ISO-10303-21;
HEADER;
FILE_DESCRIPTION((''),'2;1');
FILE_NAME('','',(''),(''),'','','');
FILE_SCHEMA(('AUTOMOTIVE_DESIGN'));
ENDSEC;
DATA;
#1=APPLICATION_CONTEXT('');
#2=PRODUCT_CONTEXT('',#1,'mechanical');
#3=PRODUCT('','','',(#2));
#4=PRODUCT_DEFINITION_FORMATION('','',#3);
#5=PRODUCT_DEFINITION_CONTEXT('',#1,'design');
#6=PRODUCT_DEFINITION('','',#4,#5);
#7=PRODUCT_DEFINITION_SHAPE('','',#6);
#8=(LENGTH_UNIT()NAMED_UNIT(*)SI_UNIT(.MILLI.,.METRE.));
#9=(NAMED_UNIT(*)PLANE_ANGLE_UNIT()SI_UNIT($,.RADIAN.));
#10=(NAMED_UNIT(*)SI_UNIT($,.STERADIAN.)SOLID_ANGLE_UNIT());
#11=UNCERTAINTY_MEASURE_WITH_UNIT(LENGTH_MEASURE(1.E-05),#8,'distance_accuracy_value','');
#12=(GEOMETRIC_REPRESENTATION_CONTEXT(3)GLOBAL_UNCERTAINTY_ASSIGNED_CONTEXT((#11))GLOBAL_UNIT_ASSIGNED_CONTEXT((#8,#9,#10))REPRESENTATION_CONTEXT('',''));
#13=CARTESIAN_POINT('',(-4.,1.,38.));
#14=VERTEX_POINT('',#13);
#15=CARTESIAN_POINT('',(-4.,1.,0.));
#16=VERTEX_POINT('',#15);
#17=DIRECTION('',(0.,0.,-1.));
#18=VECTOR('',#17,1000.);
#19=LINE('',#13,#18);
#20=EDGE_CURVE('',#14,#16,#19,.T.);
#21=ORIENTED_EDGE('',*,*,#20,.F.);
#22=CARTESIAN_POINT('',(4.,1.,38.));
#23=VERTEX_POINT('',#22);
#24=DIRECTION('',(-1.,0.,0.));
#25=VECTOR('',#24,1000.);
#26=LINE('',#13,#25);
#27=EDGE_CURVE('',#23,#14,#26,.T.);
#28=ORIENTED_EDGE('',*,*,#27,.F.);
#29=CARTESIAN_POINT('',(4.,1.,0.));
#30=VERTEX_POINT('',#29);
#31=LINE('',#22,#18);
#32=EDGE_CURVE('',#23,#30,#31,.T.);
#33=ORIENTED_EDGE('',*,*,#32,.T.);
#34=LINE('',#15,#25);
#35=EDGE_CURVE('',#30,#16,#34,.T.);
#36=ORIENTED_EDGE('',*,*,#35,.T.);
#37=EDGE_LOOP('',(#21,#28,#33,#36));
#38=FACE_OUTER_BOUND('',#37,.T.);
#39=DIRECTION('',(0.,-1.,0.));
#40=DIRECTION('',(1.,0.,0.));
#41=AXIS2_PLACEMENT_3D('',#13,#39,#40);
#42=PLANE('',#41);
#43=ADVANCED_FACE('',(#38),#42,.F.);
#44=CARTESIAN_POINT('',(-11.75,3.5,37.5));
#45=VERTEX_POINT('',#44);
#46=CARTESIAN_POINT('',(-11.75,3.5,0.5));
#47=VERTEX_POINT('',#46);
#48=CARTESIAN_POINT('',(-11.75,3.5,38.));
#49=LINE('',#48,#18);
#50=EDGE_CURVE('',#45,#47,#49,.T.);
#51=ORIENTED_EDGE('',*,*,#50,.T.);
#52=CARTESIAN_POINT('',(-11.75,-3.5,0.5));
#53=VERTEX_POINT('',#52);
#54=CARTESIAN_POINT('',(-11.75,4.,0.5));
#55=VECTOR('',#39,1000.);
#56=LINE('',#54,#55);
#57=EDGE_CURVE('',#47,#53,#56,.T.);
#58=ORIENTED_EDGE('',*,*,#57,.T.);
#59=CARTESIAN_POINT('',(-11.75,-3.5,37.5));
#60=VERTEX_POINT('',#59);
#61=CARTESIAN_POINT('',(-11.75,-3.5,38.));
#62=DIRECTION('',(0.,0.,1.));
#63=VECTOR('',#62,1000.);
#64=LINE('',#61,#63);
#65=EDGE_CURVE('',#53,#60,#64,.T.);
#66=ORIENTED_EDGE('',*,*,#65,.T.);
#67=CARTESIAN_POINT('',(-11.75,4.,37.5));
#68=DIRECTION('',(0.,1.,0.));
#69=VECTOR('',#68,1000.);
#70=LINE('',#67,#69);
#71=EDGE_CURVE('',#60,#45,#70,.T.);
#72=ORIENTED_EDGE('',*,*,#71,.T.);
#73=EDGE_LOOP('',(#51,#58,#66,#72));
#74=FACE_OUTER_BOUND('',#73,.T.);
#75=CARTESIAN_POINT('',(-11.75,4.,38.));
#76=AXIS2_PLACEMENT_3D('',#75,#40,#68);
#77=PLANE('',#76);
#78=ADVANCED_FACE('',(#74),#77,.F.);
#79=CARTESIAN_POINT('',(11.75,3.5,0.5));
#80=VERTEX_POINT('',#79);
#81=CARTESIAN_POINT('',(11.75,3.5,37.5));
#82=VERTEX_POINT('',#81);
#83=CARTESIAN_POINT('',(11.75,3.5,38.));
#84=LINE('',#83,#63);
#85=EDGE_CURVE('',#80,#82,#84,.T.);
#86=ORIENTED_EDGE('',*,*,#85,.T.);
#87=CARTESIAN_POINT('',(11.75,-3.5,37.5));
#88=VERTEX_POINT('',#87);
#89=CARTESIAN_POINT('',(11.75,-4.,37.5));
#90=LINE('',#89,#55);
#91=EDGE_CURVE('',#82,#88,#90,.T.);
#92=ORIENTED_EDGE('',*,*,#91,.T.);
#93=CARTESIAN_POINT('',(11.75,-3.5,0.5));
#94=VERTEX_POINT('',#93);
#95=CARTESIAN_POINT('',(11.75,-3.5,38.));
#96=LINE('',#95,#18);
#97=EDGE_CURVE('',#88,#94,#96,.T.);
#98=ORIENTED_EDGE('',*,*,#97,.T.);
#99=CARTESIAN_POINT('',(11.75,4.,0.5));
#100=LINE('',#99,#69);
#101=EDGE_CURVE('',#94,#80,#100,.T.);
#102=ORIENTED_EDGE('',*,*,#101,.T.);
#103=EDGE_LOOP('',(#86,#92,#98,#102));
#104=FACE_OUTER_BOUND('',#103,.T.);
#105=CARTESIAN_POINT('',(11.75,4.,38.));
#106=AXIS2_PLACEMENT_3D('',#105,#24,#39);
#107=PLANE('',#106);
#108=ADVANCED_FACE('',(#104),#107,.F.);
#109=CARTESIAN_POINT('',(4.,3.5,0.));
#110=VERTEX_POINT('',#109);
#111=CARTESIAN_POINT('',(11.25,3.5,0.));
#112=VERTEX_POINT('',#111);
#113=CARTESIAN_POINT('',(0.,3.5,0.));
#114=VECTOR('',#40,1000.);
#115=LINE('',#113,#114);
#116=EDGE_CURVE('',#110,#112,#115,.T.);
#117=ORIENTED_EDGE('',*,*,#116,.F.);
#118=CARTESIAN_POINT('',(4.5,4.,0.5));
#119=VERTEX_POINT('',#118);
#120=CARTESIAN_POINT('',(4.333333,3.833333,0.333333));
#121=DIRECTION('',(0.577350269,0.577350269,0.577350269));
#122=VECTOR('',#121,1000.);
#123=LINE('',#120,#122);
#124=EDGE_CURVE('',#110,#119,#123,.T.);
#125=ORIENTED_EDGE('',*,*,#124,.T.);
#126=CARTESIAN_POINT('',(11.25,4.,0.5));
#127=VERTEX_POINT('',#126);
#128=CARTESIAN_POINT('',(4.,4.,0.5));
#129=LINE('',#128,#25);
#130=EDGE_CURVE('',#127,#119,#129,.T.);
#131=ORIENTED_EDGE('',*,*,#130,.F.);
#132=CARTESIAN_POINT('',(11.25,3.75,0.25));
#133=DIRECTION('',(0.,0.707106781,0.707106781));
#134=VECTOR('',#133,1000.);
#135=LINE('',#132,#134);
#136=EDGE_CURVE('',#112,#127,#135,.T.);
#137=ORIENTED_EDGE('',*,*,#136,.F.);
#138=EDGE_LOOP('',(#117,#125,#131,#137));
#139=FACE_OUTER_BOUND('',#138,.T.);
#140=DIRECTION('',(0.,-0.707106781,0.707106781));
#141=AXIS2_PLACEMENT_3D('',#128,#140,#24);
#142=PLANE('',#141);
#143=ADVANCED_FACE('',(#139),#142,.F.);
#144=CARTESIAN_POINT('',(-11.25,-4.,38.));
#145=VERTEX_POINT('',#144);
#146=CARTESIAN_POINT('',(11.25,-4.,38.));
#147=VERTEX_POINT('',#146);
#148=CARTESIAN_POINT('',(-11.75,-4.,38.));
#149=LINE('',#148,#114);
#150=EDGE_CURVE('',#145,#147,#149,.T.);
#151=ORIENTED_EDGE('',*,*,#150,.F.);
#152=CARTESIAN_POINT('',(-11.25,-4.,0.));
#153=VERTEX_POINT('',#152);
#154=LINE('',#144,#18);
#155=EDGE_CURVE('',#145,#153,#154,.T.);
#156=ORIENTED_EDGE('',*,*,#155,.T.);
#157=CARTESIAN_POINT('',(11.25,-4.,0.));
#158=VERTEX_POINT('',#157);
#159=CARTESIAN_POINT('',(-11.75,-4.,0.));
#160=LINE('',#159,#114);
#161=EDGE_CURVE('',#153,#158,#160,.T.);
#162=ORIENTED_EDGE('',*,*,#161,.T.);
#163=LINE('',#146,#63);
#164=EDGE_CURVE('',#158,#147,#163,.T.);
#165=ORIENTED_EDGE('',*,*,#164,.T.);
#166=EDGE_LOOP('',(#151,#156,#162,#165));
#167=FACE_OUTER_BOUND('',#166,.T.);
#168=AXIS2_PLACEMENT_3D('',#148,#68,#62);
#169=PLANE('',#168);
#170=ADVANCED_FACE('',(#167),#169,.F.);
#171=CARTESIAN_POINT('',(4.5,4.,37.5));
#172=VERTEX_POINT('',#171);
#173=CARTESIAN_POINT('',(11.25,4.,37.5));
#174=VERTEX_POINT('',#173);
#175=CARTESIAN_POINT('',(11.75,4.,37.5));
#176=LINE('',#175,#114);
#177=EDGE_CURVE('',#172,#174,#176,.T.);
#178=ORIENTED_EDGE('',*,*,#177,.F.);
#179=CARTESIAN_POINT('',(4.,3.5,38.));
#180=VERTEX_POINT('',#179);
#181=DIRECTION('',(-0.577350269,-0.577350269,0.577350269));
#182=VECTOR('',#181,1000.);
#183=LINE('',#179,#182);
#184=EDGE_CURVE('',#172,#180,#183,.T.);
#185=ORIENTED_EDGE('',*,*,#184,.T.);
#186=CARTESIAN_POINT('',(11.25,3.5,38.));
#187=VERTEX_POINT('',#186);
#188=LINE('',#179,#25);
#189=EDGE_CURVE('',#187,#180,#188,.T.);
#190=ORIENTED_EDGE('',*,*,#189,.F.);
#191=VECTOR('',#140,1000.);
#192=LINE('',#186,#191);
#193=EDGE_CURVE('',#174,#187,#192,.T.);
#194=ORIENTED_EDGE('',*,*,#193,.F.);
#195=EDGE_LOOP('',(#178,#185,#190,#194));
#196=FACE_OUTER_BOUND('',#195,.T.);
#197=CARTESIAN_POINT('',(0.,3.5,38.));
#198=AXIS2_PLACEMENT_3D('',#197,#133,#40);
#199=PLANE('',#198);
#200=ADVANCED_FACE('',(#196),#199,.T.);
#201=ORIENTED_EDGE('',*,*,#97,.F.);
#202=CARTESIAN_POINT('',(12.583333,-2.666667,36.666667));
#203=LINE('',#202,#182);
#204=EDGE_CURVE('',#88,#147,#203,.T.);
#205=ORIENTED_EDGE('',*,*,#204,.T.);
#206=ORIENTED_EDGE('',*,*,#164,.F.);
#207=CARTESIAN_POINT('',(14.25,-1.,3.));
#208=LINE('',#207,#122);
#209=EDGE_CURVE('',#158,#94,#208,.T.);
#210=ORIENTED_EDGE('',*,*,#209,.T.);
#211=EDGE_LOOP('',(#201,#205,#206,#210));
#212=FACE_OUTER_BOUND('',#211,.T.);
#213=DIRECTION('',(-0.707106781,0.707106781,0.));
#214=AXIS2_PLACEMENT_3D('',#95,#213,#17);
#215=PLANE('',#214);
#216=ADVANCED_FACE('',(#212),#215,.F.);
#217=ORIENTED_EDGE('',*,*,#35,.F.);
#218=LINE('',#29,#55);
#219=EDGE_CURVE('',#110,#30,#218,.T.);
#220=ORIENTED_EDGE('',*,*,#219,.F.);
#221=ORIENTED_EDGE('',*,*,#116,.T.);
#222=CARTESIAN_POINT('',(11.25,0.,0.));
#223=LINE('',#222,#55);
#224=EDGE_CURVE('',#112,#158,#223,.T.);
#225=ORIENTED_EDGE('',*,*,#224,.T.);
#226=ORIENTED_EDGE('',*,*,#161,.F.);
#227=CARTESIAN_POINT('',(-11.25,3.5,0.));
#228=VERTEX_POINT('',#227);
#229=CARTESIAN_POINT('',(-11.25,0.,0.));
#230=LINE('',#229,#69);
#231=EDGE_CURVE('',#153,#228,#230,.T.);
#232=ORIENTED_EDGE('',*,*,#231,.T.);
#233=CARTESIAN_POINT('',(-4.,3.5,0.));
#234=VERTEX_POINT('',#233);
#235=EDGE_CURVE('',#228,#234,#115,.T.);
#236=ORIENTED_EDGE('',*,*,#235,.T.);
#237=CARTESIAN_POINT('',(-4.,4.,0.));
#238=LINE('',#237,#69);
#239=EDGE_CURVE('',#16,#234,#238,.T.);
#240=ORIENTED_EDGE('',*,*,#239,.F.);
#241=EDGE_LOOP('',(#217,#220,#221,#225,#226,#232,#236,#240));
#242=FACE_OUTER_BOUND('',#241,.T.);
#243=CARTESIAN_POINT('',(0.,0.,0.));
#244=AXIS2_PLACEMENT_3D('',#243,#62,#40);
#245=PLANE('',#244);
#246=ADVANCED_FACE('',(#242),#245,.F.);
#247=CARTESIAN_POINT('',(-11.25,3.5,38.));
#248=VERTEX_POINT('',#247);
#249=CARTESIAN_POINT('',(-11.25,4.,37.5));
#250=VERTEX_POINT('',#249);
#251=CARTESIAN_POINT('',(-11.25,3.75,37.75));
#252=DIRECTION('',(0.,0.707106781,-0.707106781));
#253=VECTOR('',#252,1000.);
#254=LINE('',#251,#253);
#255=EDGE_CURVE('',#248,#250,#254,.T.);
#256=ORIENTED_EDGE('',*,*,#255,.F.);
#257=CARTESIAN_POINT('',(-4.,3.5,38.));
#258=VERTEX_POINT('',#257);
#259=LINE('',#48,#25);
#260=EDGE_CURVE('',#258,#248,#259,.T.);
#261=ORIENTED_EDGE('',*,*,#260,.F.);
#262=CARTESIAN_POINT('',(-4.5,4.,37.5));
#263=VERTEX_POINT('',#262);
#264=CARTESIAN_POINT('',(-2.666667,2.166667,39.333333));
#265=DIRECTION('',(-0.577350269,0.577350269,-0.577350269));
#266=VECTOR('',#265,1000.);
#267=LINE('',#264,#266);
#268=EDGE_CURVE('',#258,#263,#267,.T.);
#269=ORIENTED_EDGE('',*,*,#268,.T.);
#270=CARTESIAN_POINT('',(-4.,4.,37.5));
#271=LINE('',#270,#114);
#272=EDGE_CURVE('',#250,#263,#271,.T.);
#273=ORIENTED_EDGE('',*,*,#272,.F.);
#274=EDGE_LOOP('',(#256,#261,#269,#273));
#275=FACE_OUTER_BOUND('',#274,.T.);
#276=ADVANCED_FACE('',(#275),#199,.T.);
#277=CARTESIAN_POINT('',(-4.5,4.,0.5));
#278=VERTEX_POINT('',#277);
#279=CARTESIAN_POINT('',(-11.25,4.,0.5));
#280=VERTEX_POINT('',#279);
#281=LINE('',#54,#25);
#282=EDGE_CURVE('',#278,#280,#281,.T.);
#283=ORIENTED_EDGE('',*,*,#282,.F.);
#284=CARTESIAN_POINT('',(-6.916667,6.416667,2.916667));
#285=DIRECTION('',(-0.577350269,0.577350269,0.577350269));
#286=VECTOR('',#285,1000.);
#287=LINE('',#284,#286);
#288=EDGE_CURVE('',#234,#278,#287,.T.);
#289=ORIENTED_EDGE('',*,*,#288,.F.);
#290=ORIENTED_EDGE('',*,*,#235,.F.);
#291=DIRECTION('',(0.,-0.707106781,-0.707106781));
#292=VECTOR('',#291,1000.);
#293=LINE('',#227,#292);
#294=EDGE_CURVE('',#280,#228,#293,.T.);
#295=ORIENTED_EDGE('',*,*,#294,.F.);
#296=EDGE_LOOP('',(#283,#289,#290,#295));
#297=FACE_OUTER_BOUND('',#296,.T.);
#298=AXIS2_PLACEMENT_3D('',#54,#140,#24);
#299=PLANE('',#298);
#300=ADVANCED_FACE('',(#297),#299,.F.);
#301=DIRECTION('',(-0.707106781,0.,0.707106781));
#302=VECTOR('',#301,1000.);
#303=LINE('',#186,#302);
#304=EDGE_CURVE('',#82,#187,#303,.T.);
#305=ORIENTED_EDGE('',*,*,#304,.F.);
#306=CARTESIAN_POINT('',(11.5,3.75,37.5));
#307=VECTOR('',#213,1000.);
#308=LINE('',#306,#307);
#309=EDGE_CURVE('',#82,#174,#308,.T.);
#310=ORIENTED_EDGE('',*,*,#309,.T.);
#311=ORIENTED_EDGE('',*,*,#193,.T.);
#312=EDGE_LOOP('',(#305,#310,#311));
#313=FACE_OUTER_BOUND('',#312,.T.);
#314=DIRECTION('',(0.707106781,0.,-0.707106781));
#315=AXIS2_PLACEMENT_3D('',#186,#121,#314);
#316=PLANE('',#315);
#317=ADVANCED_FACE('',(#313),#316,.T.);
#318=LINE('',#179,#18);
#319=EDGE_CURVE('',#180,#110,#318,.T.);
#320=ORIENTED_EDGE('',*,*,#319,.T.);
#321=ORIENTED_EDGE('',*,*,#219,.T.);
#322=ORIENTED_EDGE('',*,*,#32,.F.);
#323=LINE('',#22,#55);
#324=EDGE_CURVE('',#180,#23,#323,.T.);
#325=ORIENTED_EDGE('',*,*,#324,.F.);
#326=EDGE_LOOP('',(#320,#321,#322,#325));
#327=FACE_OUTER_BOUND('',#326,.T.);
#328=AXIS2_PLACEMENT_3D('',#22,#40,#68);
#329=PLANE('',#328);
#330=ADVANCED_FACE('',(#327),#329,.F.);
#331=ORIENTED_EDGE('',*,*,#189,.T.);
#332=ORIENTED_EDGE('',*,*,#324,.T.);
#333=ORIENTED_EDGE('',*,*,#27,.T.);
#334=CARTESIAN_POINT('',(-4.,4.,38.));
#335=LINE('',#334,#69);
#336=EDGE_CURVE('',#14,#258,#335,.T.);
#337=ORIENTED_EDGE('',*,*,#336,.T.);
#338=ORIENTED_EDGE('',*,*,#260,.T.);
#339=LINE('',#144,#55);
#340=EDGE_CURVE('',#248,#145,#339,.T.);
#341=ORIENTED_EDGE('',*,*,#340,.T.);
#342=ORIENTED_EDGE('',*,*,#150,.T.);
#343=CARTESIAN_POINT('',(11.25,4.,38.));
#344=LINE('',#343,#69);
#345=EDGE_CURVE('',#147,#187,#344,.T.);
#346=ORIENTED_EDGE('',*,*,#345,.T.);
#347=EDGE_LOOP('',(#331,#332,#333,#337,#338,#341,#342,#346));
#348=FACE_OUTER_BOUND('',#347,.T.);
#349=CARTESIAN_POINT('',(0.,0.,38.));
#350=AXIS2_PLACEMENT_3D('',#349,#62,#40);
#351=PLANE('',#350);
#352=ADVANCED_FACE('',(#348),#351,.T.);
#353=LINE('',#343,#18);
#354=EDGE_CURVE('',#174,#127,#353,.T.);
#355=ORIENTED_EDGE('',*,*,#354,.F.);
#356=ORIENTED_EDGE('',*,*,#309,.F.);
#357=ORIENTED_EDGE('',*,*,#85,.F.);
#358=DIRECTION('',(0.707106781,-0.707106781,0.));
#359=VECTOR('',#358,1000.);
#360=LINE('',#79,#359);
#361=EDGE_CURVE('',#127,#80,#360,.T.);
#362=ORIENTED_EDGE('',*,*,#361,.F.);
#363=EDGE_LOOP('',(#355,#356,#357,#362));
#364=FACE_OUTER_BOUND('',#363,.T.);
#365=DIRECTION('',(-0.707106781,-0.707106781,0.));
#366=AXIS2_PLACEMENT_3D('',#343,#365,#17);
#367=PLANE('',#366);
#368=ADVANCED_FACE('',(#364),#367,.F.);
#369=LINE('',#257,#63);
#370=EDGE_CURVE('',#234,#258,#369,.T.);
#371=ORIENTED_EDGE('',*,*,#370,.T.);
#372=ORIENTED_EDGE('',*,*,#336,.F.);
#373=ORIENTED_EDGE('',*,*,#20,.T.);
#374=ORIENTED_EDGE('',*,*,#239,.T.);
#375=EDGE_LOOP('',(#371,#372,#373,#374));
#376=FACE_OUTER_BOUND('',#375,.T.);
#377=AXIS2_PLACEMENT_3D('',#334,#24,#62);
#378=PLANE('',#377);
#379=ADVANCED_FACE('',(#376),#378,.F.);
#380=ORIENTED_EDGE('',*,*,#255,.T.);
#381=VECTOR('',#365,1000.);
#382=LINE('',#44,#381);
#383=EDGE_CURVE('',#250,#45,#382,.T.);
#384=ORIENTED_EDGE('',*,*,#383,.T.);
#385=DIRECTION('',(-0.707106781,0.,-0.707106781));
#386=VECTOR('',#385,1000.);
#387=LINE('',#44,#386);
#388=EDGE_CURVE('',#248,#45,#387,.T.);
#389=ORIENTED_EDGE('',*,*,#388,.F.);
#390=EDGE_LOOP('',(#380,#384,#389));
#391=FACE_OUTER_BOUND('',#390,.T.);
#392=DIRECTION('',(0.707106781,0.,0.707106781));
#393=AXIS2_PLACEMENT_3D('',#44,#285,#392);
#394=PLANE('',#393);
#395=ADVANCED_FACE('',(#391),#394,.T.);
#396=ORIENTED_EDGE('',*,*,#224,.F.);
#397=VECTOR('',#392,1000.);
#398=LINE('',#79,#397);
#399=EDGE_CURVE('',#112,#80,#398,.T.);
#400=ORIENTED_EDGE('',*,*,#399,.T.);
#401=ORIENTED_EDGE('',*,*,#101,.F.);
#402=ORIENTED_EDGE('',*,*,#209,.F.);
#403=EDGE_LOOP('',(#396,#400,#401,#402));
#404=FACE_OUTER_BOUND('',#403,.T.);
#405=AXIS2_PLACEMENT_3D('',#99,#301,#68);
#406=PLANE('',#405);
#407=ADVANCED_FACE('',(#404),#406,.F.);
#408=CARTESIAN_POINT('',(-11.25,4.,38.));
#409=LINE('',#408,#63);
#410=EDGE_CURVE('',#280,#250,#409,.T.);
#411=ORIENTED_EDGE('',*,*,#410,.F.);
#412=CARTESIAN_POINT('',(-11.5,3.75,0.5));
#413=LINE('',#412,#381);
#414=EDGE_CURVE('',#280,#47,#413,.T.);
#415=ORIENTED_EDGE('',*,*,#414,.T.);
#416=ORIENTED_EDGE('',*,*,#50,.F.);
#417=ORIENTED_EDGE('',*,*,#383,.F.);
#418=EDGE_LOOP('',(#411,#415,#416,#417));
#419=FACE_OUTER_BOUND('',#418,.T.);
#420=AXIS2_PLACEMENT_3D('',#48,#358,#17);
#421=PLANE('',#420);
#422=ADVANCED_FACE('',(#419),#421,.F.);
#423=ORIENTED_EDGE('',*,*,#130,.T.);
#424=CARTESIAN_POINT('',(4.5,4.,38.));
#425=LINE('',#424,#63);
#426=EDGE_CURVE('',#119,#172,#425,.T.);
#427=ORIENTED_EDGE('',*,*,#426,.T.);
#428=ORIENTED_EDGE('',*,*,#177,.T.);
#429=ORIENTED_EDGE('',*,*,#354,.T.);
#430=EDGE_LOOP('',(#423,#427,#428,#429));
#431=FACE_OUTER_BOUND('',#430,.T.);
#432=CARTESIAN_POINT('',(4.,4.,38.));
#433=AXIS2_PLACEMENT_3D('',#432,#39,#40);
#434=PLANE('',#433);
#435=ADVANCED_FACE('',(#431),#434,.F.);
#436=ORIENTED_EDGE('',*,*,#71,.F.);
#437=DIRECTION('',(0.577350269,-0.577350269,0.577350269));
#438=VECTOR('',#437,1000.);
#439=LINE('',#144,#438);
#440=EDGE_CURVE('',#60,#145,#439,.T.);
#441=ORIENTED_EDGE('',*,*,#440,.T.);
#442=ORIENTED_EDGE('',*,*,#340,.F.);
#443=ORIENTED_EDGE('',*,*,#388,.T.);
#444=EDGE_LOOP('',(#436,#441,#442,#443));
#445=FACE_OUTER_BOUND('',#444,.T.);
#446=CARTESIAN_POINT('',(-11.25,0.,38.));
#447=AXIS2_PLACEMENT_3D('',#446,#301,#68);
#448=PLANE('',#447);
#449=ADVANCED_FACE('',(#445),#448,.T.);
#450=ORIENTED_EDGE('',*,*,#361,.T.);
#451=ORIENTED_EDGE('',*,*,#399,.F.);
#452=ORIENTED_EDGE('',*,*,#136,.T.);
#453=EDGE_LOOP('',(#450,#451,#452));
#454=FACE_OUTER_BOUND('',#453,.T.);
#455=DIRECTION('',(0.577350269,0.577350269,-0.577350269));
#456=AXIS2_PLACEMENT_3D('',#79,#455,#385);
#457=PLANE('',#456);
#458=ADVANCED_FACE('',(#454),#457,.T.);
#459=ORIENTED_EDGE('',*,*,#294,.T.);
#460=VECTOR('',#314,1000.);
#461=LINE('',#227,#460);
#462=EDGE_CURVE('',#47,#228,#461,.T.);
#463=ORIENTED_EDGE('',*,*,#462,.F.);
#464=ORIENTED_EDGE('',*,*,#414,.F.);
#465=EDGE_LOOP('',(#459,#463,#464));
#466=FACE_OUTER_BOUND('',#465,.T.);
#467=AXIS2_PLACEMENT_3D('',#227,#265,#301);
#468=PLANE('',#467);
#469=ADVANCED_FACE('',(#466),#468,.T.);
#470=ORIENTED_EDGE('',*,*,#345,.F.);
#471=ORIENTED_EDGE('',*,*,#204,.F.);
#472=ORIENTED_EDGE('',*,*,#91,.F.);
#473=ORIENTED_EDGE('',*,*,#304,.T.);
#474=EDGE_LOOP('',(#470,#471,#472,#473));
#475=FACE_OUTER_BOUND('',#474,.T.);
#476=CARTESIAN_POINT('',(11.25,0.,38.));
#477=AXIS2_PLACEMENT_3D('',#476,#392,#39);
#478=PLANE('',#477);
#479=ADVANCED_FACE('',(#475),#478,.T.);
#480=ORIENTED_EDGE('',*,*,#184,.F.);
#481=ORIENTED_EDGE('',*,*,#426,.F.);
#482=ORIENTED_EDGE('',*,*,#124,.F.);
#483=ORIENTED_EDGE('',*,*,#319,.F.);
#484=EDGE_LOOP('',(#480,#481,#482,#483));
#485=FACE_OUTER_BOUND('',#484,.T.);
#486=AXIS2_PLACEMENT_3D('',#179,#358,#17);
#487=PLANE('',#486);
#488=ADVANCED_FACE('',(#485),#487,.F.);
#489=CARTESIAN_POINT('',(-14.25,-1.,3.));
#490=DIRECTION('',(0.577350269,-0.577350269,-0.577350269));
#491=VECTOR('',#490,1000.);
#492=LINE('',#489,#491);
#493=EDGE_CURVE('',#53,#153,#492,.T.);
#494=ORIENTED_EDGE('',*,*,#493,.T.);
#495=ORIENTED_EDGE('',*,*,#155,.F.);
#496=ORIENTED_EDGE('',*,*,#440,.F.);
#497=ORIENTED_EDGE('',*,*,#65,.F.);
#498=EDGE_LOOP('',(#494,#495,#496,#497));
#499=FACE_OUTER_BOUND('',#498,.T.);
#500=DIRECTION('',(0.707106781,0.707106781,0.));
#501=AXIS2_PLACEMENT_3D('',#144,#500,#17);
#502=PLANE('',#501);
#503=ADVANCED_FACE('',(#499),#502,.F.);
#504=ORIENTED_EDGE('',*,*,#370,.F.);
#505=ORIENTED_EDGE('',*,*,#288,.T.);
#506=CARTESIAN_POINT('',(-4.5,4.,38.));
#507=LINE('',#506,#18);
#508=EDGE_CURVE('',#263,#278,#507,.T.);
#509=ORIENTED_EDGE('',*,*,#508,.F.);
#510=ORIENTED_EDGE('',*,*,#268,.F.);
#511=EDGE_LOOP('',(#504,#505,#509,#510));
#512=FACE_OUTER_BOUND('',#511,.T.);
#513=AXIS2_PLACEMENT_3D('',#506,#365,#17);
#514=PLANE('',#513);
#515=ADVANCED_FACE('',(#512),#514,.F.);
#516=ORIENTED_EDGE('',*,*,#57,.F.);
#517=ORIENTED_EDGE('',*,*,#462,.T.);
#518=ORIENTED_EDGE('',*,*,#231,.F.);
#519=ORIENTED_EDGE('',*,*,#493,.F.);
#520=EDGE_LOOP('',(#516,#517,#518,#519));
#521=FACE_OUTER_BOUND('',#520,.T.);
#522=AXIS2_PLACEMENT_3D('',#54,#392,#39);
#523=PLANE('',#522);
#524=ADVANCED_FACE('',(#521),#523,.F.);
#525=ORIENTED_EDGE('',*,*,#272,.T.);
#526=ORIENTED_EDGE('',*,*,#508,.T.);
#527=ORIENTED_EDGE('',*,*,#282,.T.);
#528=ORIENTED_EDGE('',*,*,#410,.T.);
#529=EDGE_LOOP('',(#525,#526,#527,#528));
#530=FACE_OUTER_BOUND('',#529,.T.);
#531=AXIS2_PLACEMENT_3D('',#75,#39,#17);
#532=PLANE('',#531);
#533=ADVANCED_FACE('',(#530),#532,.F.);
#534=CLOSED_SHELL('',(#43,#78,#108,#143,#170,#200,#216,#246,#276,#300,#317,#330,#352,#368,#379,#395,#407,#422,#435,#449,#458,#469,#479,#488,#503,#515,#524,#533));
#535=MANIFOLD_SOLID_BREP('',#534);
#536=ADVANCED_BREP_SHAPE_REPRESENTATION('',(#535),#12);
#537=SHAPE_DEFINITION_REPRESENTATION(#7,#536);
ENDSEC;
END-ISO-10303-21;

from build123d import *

# Parameters (mm, degrees)
BOSS_EXTRUDE1_DEPTH = 38
CHAMFER1_SIZE       = 0.5


with BuildPart() as part:
    # Sketch1 → Boss-Extrude1 (new body)
    with BuildSketch(Plane.XY):
        Polygon((-11.75, 4), (-4, 4), (-4, 1), (4, 1), (4, 4), (11.75, 4), (11.75, -4), (-11.75, -4), align=None)
    extrude(amount=BOSS_EXTRUDE1_DEPTH)

    # Chamfer1
    chamfer1_edges = [part.edges().sort_by_distance(p)[0] for p in [
        (7.875, 4, 0),
        (11.75, 0, 0),
        (11.75, -4, 19),
        (-11.75, -4, 19),
        (-11.75, 4, 19),
        (-4, 4, 19),
        (4, 4, 19),
        (11.75, 4, 19),
        (-7.875, 4, 38),
        (-11.75, 0, 38),
        (11.75, 0, 38),
        (7.875, 4, 38),
        (-11.75, 0, 0),
        (-7.875, 4, 0),
    ]]
    chamfer(chamfer1_edges, length=CHAMFER1_SIZE)


solid = part.part
